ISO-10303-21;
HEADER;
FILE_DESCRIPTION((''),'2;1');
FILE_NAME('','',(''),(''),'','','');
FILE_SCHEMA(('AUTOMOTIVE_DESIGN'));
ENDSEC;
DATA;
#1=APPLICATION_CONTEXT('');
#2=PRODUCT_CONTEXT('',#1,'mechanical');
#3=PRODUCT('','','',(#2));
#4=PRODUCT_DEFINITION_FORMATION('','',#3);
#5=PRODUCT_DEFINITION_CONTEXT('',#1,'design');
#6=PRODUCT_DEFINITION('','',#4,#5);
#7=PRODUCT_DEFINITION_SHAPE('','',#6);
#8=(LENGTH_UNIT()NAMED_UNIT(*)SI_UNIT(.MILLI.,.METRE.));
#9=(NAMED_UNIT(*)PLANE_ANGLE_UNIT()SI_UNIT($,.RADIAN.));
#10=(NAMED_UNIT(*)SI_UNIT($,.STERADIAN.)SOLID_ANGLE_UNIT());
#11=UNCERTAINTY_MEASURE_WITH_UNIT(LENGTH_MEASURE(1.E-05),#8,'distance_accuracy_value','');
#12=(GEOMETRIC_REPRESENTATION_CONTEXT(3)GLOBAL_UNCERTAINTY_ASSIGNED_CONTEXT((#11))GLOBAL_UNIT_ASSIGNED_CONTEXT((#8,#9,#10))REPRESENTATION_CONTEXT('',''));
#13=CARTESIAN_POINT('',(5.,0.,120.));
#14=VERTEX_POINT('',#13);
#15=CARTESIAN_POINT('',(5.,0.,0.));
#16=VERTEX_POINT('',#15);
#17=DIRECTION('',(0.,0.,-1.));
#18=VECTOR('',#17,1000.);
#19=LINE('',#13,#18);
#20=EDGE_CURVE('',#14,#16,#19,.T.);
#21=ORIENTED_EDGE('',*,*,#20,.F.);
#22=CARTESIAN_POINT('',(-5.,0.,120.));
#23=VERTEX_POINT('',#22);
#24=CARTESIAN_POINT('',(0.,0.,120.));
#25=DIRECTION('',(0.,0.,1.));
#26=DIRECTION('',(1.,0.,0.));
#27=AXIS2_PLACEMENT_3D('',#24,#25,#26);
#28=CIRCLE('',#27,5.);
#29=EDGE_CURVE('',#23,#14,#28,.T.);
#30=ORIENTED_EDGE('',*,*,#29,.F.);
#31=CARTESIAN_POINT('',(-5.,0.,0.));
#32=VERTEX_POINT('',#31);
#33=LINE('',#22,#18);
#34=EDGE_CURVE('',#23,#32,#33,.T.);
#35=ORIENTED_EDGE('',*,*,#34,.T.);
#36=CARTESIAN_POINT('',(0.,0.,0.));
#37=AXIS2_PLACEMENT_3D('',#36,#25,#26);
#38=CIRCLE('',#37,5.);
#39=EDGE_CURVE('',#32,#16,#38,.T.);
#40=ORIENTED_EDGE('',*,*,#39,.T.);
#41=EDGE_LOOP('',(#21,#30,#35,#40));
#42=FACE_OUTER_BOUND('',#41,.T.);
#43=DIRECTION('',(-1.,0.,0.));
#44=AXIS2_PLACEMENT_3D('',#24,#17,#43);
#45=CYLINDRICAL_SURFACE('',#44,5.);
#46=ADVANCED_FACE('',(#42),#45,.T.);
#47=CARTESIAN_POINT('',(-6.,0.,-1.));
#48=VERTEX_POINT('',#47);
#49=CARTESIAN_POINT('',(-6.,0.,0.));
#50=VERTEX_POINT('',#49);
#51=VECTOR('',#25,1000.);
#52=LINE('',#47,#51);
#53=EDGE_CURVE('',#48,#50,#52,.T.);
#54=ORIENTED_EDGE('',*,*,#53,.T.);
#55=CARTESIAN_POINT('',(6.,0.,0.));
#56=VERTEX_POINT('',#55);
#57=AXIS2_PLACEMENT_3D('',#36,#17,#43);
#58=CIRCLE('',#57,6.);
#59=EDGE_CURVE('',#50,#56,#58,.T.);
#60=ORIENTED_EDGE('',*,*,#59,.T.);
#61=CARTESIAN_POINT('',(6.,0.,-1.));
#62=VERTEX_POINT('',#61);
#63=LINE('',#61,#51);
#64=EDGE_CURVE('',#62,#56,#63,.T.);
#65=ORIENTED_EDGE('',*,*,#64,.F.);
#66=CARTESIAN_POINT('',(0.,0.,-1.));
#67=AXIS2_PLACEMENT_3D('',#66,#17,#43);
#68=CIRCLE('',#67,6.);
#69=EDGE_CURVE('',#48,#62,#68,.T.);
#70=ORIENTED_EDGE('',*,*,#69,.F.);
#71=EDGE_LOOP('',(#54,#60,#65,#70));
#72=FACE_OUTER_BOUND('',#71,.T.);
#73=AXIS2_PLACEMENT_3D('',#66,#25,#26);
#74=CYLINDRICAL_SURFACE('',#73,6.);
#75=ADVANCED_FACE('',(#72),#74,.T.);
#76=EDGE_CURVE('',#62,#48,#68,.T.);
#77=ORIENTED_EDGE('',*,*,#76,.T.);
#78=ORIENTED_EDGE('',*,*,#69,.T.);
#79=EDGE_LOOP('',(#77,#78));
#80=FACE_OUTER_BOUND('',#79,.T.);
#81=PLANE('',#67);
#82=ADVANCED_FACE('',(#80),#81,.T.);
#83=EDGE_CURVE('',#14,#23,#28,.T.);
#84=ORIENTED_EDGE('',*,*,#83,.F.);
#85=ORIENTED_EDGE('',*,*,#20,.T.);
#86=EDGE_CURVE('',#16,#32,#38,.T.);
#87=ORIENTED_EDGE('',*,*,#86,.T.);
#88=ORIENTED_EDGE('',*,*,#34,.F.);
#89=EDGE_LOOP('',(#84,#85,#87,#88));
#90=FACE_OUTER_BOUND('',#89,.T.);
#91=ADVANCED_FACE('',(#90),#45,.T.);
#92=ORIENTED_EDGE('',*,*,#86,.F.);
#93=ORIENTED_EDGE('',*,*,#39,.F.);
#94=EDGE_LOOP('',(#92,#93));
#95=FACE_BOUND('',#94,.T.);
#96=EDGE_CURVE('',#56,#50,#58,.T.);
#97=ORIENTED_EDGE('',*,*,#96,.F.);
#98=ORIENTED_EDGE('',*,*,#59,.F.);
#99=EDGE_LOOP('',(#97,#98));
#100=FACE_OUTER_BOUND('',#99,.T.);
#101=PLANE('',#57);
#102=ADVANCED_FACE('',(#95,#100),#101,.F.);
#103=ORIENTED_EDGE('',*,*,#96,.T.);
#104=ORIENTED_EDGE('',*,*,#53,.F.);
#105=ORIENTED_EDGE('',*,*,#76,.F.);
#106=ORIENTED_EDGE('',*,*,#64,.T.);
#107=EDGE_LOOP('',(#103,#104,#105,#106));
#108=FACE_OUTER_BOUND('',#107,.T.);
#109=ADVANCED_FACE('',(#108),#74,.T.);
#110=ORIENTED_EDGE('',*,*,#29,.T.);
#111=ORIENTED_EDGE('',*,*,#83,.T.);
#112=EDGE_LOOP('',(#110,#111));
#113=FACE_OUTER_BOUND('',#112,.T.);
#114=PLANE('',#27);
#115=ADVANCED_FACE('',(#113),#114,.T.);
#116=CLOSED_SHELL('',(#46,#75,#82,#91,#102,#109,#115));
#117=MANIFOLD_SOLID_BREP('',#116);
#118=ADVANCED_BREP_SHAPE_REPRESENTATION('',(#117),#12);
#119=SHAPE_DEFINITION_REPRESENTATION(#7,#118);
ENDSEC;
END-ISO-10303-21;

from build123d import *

# Parameters (mm, degrees)
SKETCH_1_R      = 5
EXTRUDE_1_DEPTH = 120
SKETCH_2_R      = 6
EXTRUDE_2_DEPTH = 1


with BuildPart() as part:
    # 草图1 → 凸台-拉伸1 (new body)
    with BuildSketch(Plane.XY):
        Circle(SKETCH_1_R)
    extrude(amount=EXTRUDE_1_DEPTH)

    # 草图2 → 凸台-拉伸2 (add)
    with BuildSketch(Plane(origin=(0, 0, 0), x_dir=(-1, 0, 0), z_dir=(0, 0, -1))):
        Circle(SKETCH_2_R)
    extrude(amount=EXTRUDE_2_DEPTH)


solid = part.part
